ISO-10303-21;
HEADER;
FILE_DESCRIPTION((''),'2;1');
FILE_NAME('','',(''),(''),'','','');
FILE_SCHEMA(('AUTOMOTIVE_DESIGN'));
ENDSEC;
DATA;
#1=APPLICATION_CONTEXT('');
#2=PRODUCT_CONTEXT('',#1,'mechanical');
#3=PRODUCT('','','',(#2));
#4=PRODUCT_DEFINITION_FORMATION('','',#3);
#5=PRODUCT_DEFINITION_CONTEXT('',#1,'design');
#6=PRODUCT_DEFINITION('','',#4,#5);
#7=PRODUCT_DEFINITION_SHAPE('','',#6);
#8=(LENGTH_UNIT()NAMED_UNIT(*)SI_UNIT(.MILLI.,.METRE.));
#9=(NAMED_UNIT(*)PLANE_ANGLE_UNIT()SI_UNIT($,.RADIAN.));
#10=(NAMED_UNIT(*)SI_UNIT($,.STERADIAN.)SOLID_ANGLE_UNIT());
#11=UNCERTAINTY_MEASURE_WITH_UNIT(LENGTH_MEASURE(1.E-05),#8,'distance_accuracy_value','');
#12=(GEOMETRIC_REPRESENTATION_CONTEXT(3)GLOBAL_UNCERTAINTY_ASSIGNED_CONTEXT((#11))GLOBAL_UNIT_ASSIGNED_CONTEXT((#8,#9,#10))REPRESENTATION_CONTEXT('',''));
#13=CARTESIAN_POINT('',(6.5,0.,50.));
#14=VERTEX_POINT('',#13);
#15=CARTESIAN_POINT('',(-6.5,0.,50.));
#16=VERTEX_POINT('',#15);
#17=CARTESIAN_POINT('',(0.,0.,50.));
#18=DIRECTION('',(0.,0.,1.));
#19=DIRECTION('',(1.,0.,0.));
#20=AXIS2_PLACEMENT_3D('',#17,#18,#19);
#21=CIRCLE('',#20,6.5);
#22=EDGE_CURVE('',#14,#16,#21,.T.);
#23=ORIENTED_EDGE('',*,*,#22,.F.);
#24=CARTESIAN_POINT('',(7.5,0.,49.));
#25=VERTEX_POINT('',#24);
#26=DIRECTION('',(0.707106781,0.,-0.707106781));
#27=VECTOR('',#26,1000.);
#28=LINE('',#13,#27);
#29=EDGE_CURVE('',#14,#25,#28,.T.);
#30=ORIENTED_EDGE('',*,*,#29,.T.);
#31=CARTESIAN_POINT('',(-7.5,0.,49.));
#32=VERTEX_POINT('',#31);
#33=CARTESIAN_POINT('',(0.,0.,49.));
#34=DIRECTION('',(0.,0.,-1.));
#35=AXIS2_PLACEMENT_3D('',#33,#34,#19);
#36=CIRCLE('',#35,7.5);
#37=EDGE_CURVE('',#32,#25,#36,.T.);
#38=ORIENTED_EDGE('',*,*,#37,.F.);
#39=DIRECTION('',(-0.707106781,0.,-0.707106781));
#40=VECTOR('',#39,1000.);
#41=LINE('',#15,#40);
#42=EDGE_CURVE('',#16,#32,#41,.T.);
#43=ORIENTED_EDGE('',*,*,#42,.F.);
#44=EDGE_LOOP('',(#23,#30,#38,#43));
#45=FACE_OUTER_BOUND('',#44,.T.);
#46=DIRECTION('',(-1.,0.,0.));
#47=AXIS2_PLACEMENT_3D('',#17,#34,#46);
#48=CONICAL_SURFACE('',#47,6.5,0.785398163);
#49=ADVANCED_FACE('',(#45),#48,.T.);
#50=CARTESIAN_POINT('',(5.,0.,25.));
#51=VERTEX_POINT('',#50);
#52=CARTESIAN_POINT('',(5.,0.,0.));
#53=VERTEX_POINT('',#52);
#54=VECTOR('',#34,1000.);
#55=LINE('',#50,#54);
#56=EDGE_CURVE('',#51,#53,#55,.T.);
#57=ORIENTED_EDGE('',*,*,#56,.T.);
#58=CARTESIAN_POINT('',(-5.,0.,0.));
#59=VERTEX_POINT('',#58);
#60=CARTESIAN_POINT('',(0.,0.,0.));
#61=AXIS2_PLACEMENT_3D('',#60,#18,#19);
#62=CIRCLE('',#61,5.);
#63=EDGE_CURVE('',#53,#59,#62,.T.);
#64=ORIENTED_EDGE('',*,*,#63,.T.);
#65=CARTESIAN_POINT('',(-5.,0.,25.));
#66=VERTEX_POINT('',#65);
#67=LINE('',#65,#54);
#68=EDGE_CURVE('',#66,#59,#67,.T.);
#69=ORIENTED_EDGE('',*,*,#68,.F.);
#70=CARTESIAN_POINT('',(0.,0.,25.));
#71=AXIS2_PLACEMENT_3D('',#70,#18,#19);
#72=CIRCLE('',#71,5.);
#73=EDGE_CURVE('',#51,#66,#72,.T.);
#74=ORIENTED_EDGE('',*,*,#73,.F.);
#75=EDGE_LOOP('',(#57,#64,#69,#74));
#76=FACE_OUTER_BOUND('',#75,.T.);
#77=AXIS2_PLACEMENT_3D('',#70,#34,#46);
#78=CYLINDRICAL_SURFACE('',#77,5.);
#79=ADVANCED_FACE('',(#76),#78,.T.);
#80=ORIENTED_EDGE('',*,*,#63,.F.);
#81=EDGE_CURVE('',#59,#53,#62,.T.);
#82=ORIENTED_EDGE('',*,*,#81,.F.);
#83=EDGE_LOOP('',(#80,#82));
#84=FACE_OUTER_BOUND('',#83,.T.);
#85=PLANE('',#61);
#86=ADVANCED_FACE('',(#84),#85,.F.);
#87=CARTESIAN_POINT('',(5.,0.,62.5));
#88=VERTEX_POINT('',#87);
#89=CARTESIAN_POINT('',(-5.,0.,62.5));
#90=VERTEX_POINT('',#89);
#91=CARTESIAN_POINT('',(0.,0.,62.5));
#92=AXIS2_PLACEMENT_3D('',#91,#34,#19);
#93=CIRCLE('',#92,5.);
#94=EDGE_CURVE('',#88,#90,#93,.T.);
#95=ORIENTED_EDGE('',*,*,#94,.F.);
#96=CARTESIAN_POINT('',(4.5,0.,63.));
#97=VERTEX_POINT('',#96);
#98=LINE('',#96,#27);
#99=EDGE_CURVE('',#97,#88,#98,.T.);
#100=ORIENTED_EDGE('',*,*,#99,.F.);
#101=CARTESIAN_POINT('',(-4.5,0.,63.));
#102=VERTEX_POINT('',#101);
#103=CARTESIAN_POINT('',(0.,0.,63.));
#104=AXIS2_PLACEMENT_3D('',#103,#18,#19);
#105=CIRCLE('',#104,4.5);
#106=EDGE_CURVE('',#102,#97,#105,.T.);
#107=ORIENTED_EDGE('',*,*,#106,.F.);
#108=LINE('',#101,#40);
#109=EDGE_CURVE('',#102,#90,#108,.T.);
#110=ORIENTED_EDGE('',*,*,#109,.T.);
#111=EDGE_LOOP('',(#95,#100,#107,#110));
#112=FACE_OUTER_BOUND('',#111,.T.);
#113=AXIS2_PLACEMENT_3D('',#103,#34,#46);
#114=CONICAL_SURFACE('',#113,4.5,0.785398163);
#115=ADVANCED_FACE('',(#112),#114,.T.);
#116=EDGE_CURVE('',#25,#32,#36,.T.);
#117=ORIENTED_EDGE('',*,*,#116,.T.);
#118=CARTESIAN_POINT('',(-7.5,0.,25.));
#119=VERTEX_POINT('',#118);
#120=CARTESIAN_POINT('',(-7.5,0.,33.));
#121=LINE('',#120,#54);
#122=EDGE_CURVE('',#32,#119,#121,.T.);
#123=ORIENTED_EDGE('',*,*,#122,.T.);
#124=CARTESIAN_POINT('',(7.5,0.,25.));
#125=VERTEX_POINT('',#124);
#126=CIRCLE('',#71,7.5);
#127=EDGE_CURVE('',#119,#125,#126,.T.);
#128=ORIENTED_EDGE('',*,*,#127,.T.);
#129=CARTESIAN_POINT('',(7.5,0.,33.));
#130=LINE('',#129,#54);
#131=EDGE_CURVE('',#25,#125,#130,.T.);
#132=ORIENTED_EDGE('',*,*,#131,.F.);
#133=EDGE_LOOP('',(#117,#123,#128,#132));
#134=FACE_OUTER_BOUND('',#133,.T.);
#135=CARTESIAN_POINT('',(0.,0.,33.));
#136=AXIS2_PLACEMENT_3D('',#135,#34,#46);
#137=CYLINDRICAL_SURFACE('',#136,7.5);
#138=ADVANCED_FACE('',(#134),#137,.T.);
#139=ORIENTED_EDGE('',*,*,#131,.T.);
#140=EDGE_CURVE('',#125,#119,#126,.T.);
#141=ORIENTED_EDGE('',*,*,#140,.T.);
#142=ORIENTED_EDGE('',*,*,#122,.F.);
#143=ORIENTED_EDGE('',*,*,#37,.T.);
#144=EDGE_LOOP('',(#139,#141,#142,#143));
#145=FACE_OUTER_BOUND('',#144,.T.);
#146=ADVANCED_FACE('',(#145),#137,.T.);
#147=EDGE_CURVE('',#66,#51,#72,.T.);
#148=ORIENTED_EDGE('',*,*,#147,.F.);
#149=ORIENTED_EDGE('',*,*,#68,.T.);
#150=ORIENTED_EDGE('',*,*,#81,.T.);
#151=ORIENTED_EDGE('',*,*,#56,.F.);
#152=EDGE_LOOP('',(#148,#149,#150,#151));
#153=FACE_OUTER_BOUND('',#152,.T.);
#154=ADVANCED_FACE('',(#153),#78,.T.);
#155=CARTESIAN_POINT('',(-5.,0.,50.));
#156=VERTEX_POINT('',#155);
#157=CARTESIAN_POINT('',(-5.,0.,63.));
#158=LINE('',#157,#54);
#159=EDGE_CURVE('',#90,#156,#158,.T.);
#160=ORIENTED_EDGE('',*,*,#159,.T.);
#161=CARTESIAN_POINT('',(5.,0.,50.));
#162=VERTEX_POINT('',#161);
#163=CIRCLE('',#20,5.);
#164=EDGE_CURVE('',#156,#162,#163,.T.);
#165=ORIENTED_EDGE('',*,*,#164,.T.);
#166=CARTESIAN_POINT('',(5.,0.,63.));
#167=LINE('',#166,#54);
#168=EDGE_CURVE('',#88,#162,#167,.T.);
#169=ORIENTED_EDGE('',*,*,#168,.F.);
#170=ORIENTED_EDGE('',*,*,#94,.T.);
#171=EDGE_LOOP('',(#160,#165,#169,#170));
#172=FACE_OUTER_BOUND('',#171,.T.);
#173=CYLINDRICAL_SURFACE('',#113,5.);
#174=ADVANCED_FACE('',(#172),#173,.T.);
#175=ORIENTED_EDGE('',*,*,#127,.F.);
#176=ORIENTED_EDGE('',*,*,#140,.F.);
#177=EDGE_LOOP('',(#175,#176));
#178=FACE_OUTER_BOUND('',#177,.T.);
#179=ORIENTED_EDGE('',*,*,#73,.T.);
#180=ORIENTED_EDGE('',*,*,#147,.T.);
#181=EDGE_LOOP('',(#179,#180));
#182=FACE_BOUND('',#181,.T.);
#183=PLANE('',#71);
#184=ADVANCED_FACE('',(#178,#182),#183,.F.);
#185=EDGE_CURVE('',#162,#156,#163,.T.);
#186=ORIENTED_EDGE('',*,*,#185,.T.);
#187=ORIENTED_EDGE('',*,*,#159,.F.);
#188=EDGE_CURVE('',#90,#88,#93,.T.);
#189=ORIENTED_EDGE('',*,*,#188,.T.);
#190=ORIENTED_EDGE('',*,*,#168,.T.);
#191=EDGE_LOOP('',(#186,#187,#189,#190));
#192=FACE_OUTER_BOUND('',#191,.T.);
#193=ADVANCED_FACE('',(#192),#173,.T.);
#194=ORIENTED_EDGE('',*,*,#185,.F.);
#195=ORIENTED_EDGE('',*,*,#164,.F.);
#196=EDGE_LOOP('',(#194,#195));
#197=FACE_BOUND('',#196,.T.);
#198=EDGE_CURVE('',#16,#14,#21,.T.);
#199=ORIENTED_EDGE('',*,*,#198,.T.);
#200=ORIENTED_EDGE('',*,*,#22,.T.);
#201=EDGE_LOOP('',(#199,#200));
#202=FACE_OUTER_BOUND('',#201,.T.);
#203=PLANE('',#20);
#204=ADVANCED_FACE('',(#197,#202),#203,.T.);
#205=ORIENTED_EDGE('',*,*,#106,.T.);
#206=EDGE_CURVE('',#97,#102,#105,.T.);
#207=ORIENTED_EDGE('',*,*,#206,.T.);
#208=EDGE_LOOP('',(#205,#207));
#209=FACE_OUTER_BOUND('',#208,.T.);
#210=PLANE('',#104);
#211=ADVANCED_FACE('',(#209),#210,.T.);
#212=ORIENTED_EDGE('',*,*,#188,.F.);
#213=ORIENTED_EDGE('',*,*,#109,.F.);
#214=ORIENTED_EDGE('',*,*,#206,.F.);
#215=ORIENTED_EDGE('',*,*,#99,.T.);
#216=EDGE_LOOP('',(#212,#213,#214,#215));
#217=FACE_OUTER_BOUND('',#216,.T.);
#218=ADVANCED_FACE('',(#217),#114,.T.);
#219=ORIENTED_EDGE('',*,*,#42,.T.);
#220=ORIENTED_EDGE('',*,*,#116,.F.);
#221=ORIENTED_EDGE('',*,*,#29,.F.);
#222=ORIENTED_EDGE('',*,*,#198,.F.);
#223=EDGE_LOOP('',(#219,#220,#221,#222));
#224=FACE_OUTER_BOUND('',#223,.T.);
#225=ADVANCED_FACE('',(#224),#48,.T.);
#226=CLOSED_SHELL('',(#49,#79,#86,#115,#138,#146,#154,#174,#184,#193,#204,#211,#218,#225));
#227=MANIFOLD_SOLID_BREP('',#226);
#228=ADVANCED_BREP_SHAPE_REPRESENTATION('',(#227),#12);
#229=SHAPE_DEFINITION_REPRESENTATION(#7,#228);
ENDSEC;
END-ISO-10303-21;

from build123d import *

# Parameters (mm, degrees)
SKETCH1_R           = 5
BOSS_EXTRUDE1_DEPTH = 25
SKETCH2_R           = 7.5
BOSS_EXTRUDE2_DEPTH = 8
SKETCH3_R           = 5
BOSS_EXTRUDE3_DEPTH = 30
SKETCH4_R           = 7.5
BOSS_EXTRUDE4_DEPTH = 17
CHAMFER1_SIZE       = 1
CHAMFER2_SIZE       = 0.5


with BuildPart() as part:
    # Sketch1 → Boss-Extrude1 (new body)
    with BuildSketch(Plane.XY):
        Circle(SKETCH1_R)
    extrude(amount=BOSS_EXTRUDE1_DEPTH)

    # Sketch2 → Boss-Extrude2 (add)
    with BuildSketch(Plane.XY.offset(25)):
        Circle(SKETCH2_R)
    extrude(amount=BOSS_EXTRUDE2_DEPTH)

    # Sketch3 → Boss-Extrude3 (add)
    with BuildSketch(Plane.XY.offset(33)):
        Circle(SKETCH3_R)
    extrude(amount=BOSS_EXTRUDE3_DEPTH)

    # Sketch4 → Boss-Extrude4 (add)
    with BuildSketch(Plane.XY.offset(33)):
        Circle(SKETCH4_R)
    extrude(amount=BOSS_EXTRUDE4_DEPTH)

    # Chamfer1
    chamfer1_edges = [part.edges().sort_by_distance(p)[0] for p in [
        (-7.5, 0, 50),
    ]]
    chamfer(chamfer1_edges, length=CHAMFER1_SIZE)

    # Chamfer2
    chamfer2_edges = [part.edges().sort_by_distance(p)[0] for p in [
        (-5, 0, 63),
    ]]
    chamfer(chamfer2_edges, length=CHAMFER2_SIZE)


solid = part.part
